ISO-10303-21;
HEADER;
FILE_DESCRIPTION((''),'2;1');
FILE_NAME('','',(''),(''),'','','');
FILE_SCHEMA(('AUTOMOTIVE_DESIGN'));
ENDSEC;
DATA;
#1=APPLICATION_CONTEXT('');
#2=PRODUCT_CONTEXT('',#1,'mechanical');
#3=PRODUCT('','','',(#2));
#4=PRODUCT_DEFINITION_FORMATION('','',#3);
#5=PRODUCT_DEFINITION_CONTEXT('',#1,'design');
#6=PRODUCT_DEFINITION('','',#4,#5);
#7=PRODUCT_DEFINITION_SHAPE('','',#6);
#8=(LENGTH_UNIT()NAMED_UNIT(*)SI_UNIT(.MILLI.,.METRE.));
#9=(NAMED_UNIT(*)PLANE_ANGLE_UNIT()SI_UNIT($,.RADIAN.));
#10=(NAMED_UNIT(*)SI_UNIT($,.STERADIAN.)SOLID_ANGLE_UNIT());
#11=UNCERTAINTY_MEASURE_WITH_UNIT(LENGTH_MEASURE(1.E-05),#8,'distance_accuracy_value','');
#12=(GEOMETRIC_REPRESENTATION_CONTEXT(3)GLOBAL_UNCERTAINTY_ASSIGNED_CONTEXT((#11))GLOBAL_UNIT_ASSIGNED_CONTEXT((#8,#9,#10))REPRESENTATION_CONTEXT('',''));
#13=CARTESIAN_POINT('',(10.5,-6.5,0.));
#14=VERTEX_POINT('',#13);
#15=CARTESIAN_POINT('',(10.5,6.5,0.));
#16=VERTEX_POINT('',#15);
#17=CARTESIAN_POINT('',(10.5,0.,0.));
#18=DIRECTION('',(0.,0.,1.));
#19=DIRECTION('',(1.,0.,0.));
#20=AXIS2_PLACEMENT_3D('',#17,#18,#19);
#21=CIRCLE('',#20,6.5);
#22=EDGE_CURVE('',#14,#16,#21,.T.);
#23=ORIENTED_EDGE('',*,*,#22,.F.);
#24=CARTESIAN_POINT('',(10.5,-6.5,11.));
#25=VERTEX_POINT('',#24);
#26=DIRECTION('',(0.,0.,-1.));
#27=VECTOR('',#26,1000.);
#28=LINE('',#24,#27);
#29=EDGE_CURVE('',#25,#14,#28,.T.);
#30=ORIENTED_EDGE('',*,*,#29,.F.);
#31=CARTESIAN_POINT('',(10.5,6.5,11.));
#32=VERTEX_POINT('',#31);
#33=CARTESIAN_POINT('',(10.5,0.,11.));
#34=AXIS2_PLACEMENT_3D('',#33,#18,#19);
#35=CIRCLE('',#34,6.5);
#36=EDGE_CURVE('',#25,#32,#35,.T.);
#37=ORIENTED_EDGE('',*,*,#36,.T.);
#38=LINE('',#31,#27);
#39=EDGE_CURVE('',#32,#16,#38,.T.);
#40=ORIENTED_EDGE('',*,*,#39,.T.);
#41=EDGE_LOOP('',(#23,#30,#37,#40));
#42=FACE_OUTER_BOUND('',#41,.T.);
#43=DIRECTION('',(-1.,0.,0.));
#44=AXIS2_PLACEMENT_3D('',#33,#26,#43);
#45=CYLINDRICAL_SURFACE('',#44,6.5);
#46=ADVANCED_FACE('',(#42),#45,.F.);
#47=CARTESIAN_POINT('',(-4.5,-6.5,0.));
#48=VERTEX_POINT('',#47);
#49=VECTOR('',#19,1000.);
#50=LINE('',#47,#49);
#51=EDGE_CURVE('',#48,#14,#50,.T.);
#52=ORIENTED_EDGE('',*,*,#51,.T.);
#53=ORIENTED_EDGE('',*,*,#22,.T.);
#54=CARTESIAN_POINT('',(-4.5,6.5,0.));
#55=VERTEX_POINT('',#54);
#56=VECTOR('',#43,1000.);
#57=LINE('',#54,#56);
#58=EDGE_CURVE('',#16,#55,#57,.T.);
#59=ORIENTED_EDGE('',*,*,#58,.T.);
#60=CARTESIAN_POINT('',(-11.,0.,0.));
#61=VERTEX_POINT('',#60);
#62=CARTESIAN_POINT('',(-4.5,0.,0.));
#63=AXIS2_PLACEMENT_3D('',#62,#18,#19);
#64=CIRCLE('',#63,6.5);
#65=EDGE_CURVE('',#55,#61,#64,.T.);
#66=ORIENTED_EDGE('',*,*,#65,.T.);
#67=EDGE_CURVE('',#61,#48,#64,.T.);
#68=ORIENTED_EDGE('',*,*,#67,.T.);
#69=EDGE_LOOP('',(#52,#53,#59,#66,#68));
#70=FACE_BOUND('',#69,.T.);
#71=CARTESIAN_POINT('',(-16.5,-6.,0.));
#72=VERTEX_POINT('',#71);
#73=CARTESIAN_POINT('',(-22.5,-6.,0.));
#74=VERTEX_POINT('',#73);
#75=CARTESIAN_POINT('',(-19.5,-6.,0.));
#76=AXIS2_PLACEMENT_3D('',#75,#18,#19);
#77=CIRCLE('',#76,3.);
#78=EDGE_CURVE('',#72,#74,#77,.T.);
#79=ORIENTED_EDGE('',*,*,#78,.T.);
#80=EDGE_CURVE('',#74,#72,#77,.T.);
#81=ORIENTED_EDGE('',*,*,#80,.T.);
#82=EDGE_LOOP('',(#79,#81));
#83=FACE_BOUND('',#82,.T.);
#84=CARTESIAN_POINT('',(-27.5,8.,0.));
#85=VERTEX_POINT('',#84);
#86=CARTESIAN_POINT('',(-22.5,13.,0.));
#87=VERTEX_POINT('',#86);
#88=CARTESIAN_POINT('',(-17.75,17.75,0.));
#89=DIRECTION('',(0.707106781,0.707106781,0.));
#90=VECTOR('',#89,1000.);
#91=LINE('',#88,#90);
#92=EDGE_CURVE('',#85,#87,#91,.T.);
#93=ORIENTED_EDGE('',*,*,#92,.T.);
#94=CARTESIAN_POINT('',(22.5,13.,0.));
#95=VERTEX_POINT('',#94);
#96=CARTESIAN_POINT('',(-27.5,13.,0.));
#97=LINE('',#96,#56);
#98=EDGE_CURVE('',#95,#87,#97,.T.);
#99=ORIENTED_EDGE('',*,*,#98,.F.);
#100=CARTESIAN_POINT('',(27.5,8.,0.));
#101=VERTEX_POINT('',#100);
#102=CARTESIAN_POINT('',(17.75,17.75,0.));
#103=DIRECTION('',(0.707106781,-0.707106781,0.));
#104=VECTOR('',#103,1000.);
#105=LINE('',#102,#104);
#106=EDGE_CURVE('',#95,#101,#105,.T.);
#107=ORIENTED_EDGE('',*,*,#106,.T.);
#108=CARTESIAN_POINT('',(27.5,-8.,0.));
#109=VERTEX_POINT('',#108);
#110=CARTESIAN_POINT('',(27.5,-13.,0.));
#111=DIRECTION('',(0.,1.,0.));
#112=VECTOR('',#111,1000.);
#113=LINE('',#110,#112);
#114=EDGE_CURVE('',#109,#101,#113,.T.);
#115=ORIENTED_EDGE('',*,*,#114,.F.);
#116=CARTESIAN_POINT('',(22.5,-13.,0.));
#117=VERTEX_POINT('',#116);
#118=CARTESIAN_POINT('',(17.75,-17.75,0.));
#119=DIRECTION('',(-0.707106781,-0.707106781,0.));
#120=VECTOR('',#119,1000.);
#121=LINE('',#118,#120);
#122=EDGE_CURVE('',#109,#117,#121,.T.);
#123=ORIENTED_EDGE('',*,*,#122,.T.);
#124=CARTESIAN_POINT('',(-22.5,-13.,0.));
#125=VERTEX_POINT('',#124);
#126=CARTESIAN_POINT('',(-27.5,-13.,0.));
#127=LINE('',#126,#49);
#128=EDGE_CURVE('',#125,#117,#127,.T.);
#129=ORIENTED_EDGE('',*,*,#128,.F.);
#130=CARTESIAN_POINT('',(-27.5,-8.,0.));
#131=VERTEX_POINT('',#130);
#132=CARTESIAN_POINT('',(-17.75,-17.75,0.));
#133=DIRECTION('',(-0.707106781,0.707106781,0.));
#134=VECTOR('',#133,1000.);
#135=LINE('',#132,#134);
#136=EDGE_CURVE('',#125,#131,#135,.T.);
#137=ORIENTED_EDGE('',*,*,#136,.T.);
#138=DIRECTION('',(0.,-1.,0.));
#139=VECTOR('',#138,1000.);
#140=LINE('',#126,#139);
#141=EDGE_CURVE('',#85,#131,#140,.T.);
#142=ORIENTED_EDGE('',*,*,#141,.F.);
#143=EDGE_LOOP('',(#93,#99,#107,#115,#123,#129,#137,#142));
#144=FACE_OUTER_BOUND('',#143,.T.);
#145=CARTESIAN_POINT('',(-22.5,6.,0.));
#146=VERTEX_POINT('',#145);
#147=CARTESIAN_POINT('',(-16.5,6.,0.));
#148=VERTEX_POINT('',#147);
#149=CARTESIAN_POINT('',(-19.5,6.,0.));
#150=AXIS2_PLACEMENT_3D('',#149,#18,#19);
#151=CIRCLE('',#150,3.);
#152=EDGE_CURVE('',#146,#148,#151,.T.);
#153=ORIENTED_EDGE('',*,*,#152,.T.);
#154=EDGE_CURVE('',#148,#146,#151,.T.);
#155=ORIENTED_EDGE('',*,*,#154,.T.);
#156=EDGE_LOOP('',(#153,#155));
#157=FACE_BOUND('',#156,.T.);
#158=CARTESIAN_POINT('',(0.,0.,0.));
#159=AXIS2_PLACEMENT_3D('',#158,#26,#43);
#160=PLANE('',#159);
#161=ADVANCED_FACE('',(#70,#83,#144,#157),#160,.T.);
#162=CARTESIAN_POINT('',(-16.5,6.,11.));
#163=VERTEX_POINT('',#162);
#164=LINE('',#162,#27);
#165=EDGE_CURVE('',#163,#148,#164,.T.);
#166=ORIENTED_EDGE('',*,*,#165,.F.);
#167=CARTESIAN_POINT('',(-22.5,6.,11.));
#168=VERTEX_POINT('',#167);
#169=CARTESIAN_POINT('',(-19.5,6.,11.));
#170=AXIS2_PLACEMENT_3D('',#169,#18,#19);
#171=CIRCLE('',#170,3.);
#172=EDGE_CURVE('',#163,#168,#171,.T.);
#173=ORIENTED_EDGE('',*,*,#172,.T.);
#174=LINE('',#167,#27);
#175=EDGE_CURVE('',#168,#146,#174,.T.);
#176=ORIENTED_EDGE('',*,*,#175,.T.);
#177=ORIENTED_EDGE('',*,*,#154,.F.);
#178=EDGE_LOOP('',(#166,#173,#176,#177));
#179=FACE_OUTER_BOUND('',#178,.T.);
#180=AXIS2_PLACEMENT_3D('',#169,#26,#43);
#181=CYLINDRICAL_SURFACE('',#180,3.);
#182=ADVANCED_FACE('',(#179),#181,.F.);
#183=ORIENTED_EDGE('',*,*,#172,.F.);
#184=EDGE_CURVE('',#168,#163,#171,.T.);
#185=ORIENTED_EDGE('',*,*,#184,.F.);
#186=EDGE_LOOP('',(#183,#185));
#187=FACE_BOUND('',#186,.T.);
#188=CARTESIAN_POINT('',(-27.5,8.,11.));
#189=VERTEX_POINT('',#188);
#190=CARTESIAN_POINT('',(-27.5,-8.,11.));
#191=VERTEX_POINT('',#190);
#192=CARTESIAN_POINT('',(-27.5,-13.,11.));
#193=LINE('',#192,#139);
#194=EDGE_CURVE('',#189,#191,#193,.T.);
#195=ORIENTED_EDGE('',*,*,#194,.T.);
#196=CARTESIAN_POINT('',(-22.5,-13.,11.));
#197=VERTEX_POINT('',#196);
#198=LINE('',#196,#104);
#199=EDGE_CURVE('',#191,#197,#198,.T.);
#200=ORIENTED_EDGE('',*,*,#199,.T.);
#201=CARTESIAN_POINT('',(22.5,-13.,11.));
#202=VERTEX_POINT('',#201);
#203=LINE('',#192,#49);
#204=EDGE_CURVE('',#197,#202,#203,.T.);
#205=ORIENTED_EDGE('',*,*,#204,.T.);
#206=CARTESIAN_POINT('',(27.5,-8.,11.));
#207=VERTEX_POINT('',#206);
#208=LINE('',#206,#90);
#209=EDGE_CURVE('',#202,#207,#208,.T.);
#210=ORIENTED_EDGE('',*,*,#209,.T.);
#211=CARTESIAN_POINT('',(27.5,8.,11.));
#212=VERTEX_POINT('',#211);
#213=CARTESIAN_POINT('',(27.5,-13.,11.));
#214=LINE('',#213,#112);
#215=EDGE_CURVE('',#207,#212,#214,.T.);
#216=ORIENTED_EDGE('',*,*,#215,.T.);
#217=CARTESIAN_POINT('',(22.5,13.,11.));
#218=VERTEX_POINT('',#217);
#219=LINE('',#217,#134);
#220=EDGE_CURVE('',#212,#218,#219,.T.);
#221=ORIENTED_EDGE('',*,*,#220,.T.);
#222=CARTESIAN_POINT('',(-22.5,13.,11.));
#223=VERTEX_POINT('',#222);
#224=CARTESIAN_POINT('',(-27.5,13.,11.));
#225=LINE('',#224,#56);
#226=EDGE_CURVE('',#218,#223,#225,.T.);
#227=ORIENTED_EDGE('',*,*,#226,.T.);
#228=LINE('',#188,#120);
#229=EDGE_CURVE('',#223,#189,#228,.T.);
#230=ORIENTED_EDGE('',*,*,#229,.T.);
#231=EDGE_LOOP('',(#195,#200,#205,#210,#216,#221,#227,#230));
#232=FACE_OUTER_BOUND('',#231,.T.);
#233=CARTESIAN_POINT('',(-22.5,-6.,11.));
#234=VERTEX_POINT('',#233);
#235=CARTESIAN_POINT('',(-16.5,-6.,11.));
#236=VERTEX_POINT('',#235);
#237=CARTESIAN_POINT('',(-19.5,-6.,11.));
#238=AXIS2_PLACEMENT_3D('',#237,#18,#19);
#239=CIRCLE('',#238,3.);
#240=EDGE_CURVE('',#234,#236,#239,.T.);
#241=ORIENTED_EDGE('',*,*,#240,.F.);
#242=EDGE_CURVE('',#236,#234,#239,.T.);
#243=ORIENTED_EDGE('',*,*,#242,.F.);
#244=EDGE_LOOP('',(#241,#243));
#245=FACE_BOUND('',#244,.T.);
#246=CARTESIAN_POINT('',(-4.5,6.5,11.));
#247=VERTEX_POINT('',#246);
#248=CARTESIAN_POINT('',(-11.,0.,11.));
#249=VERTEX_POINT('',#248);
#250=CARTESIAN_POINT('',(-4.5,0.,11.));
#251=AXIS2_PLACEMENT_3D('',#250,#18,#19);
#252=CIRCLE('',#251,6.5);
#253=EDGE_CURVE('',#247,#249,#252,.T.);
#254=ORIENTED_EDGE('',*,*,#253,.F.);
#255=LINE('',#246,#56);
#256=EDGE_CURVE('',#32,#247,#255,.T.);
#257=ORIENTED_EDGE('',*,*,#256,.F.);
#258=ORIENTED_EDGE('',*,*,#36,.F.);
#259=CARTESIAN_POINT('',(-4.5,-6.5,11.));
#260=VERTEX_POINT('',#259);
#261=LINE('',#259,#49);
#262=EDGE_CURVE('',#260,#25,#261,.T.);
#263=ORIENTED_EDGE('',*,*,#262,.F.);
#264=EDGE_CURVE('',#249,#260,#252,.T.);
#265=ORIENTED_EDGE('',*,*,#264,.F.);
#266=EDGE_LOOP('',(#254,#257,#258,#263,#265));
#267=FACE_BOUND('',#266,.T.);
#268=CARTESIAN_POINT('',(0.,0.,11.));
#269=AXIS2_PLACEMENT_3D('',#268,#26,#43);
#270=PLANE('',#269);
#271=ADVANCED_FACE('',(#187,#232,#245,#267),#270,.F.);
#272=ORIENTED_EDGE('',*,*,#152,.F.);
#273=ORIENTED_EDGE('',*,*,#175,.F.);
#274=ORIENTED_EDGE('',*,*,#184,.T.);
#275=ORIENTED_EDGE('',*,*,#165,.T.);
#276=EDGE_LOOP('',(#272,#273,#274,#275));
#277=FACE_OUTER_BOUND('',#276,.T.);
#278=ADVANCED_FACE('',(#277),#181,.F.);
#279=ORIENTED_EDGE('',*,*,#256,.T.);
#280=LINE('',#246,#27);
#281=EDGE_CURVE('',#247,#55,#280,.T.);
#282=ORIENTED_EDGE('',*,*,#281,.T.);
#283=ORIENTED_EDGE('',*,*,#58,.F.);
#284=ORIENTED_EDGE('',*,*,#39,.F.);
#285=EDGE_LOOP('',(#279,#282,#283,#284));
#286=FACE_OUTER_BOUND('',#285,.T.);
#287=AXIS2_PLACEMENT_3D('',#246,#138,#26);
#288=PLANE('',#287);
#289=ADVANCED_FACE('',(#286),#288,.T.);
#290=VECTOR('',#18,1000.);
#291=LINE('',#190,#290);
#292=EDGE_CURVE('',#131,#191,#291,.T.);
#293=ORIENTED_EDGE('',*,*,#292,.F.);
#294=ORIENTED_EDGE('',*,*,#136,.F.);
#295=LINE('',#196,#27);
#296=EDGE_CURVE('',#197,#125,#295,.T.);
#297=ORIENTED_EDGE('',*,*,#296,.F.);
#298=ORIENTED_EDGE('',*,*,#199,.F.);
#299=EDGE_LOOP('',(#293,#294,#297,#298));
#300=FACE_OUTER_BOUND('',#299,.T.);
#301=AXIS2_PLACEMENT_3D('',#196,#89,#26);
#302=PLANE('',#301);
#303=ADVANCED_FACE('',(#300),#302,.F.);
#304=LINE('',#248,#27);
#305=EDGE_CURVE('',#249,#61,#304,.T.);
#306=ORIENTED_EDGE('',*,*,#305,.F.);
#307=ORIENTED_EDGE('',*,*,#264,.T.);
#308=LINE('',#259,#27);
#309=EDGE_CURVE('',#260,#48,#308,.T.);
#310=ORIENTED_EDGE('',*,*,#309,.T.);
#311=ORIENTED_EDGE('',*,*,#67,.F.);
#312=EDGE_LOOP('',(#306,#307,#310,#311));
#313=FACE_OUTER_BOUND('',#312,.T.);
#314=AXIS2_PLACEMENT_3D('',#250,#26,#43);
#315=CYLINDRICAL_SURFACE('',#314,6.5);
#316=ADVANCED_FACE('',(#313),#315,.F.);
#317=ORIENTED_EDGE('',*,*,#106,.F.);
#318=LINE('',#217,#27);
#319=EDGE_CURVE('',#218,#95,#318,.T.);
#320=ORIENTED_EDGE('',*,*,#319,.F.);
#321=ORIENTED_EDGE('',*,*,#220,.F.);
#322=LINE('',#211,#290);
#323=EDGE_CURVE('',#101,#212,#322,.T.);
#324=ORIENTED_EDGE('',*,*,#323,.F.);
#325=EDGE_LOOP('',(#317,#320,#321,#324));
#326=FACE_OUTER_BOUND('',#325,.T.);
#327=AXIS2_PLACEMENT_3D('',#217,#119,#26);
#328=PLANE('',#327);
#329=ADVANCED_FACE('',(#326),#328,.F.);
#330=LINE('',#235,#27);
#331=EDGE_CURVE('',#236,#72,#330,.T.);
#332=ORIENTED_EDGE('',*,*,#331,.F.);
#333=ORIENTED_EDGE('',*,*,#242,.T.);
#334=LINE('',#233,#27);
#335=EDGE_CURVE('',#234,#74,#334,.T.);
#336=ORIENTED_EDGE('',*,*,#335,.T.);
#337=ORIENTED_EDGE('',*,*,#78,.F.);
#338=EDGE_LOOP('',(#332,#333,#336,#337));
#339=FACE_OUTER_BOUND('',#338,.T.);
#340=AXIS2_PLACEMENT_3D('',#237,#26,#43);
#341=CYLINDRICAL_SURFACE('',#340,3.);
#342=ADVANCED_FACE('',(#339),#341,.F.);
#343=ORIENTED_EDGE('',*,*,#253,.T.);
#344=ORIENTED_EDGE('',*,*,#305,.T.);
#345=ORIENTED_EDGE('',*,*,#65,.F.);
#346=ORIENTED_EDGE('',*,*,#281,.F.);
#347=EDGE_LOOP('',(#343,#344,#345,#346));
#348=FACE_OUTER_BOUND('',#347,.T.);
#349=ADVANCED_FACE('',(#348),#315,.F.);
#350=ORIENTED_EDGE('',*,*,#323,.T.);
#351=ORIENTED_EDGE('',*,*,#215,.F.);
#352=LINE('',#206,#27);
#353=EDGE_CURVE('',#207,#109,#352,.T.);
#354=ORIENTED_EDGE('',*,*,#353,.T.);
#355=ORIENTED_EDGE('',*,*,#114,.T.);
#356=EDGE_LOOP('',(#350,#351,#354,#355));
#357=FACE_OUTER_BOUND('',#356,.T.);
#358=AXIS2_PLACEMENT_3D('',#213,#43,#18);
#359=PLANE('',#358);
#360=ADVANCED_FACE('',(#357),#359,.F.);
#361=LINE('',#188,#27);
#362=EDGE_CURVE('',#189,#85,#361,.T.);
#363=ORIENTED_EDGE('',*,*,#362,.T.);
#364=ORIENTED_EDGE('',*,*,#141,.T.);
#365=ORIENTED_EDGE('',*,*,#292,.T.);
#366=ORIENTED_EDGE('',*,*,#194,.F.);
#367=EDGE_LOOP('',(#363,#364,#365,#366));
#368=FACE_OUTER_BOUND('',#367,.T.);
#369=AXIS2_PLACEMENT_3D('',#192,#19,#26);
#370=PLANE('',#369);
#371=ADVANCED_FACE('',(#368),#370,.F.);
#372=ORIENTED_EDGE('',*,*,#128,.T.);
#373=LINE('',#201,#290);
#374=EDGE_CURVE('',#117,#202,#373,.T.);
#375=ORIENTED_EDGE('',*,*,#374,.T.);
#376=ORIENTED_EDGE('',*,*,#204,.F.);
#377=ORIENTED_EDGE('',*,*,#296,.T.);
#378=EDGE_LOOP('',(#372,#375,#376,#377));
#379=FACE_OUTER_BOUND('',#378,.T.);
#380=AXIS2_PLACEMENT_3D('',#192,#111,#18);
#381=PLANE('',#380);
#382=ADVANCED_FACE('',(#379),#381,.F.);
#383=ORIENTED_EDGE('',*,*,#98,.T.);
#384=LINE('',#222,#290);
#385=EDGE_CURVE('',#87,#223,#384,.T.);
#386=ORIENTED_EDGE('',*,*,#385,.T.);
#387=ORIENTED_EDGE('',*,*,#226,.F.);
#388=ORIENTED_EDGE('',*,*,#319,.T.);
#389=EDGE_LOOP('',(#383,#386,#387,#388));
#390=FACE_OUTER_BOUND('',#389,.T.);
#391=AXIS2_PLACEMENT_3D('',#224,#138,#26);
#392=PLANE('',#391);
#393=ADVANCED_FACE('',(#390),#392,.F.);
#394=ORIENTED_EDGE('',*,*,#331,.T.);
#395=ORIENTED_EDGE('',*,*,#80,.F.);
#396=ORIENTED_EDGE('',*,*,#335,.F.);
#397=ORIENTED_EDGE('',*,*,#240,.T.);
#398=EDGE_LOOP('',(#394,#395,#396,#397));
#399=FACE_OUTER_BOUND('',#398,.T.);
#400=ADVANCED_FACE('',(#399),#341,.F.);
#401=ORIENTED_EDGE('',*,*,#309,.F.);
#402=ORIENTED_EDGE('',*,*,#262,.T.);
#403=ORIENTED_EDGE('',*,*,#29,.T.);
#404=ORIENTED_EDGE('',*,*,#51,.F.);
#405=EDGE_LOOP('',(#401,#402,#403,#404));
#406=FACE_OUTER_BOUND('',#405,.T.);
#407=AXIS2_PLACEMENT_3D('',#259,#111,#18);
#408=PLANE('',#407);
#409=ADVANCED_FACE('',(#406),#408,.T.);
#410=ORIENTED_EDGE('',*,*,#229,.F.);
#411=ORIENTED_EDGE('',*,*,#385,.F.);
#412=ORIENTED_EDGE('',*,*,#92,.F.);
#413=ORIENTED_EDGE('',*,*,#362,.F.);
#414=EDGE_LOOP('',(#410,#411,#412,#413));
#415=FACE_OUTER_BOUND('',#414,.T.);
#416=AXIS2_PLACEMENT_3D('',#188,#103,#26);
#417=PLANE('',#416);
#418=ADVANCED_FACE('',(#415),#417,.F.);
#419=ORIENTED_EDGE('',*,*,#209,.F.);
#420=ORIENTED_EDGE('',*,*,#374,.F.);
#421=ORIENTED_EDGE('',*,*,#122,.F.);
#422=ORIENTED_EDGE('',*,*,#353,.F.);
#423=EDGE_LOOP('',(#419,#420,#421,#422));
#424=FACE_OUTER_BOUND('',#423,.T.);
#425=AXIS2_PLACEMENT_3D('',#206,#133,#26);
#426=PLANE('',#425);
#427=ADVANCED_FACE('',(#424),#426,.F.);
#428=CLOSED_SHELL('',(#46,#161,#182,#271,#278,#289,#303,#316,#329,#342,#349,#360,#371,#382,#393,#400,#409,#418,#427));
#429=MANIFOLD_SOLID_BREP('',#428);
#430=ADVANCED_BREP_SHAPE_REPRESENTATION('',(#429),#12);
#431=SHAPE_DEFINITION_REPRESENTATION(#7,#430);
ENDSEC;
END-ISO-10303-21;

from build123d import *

# Parameters (mm, degrees)
SKETCH_1_W      = 55
SKETCH_1_H      = 26
SKETCH_1_R      = 3
EXTRUDE_1_DEPTH = 11
CHAMFER_1_SIZE  = 5


with BuildPart() as part:
    # 草图1 → 凸台-拉伸1 (new body)
    with BuildSketch(Plane.XY):
        Rectangle(SKETCH_1_W, SKETCH_1_H)
        with Locations((-19.5, 6)):
            Circle(SKETCH_1_R, mode=Mode.SUBTRACT)
        with Locations((-19.5, -6)):
            Circle(SKETCH_1_R, mode=Mode.SUBTRACT)
        with BuildLine():
            Line((-4.5, 6.5), (10.5, 6.5))
            ThreePointArc((10.5, 6.5), (17, 0), (10.5, -6.5))
            Line((10.5, -6.5), (-4.5, -6.5))
            ThreePointArc((-4.5, -6.5), (-11, 0), (-4.5, 6.5))
        make_face(mode=Mode.SUBTRACT)
    extrude(amount=EXTRUDE_1_DEPTH)

    # 倒角1
    chamfer_1_edges = [part.edges().sort_by_distance(p)[0] for p in [
        (27.5, -13, 5.5),
        (-27.5, -13, 5.5),
        (-27.5, 13, 5.5),
        (27.5, 13, 5.5),
    ]]
    chamfer(chamfer_1_edges, length=CHAMFER_1_SIZE)


solid = part.part
